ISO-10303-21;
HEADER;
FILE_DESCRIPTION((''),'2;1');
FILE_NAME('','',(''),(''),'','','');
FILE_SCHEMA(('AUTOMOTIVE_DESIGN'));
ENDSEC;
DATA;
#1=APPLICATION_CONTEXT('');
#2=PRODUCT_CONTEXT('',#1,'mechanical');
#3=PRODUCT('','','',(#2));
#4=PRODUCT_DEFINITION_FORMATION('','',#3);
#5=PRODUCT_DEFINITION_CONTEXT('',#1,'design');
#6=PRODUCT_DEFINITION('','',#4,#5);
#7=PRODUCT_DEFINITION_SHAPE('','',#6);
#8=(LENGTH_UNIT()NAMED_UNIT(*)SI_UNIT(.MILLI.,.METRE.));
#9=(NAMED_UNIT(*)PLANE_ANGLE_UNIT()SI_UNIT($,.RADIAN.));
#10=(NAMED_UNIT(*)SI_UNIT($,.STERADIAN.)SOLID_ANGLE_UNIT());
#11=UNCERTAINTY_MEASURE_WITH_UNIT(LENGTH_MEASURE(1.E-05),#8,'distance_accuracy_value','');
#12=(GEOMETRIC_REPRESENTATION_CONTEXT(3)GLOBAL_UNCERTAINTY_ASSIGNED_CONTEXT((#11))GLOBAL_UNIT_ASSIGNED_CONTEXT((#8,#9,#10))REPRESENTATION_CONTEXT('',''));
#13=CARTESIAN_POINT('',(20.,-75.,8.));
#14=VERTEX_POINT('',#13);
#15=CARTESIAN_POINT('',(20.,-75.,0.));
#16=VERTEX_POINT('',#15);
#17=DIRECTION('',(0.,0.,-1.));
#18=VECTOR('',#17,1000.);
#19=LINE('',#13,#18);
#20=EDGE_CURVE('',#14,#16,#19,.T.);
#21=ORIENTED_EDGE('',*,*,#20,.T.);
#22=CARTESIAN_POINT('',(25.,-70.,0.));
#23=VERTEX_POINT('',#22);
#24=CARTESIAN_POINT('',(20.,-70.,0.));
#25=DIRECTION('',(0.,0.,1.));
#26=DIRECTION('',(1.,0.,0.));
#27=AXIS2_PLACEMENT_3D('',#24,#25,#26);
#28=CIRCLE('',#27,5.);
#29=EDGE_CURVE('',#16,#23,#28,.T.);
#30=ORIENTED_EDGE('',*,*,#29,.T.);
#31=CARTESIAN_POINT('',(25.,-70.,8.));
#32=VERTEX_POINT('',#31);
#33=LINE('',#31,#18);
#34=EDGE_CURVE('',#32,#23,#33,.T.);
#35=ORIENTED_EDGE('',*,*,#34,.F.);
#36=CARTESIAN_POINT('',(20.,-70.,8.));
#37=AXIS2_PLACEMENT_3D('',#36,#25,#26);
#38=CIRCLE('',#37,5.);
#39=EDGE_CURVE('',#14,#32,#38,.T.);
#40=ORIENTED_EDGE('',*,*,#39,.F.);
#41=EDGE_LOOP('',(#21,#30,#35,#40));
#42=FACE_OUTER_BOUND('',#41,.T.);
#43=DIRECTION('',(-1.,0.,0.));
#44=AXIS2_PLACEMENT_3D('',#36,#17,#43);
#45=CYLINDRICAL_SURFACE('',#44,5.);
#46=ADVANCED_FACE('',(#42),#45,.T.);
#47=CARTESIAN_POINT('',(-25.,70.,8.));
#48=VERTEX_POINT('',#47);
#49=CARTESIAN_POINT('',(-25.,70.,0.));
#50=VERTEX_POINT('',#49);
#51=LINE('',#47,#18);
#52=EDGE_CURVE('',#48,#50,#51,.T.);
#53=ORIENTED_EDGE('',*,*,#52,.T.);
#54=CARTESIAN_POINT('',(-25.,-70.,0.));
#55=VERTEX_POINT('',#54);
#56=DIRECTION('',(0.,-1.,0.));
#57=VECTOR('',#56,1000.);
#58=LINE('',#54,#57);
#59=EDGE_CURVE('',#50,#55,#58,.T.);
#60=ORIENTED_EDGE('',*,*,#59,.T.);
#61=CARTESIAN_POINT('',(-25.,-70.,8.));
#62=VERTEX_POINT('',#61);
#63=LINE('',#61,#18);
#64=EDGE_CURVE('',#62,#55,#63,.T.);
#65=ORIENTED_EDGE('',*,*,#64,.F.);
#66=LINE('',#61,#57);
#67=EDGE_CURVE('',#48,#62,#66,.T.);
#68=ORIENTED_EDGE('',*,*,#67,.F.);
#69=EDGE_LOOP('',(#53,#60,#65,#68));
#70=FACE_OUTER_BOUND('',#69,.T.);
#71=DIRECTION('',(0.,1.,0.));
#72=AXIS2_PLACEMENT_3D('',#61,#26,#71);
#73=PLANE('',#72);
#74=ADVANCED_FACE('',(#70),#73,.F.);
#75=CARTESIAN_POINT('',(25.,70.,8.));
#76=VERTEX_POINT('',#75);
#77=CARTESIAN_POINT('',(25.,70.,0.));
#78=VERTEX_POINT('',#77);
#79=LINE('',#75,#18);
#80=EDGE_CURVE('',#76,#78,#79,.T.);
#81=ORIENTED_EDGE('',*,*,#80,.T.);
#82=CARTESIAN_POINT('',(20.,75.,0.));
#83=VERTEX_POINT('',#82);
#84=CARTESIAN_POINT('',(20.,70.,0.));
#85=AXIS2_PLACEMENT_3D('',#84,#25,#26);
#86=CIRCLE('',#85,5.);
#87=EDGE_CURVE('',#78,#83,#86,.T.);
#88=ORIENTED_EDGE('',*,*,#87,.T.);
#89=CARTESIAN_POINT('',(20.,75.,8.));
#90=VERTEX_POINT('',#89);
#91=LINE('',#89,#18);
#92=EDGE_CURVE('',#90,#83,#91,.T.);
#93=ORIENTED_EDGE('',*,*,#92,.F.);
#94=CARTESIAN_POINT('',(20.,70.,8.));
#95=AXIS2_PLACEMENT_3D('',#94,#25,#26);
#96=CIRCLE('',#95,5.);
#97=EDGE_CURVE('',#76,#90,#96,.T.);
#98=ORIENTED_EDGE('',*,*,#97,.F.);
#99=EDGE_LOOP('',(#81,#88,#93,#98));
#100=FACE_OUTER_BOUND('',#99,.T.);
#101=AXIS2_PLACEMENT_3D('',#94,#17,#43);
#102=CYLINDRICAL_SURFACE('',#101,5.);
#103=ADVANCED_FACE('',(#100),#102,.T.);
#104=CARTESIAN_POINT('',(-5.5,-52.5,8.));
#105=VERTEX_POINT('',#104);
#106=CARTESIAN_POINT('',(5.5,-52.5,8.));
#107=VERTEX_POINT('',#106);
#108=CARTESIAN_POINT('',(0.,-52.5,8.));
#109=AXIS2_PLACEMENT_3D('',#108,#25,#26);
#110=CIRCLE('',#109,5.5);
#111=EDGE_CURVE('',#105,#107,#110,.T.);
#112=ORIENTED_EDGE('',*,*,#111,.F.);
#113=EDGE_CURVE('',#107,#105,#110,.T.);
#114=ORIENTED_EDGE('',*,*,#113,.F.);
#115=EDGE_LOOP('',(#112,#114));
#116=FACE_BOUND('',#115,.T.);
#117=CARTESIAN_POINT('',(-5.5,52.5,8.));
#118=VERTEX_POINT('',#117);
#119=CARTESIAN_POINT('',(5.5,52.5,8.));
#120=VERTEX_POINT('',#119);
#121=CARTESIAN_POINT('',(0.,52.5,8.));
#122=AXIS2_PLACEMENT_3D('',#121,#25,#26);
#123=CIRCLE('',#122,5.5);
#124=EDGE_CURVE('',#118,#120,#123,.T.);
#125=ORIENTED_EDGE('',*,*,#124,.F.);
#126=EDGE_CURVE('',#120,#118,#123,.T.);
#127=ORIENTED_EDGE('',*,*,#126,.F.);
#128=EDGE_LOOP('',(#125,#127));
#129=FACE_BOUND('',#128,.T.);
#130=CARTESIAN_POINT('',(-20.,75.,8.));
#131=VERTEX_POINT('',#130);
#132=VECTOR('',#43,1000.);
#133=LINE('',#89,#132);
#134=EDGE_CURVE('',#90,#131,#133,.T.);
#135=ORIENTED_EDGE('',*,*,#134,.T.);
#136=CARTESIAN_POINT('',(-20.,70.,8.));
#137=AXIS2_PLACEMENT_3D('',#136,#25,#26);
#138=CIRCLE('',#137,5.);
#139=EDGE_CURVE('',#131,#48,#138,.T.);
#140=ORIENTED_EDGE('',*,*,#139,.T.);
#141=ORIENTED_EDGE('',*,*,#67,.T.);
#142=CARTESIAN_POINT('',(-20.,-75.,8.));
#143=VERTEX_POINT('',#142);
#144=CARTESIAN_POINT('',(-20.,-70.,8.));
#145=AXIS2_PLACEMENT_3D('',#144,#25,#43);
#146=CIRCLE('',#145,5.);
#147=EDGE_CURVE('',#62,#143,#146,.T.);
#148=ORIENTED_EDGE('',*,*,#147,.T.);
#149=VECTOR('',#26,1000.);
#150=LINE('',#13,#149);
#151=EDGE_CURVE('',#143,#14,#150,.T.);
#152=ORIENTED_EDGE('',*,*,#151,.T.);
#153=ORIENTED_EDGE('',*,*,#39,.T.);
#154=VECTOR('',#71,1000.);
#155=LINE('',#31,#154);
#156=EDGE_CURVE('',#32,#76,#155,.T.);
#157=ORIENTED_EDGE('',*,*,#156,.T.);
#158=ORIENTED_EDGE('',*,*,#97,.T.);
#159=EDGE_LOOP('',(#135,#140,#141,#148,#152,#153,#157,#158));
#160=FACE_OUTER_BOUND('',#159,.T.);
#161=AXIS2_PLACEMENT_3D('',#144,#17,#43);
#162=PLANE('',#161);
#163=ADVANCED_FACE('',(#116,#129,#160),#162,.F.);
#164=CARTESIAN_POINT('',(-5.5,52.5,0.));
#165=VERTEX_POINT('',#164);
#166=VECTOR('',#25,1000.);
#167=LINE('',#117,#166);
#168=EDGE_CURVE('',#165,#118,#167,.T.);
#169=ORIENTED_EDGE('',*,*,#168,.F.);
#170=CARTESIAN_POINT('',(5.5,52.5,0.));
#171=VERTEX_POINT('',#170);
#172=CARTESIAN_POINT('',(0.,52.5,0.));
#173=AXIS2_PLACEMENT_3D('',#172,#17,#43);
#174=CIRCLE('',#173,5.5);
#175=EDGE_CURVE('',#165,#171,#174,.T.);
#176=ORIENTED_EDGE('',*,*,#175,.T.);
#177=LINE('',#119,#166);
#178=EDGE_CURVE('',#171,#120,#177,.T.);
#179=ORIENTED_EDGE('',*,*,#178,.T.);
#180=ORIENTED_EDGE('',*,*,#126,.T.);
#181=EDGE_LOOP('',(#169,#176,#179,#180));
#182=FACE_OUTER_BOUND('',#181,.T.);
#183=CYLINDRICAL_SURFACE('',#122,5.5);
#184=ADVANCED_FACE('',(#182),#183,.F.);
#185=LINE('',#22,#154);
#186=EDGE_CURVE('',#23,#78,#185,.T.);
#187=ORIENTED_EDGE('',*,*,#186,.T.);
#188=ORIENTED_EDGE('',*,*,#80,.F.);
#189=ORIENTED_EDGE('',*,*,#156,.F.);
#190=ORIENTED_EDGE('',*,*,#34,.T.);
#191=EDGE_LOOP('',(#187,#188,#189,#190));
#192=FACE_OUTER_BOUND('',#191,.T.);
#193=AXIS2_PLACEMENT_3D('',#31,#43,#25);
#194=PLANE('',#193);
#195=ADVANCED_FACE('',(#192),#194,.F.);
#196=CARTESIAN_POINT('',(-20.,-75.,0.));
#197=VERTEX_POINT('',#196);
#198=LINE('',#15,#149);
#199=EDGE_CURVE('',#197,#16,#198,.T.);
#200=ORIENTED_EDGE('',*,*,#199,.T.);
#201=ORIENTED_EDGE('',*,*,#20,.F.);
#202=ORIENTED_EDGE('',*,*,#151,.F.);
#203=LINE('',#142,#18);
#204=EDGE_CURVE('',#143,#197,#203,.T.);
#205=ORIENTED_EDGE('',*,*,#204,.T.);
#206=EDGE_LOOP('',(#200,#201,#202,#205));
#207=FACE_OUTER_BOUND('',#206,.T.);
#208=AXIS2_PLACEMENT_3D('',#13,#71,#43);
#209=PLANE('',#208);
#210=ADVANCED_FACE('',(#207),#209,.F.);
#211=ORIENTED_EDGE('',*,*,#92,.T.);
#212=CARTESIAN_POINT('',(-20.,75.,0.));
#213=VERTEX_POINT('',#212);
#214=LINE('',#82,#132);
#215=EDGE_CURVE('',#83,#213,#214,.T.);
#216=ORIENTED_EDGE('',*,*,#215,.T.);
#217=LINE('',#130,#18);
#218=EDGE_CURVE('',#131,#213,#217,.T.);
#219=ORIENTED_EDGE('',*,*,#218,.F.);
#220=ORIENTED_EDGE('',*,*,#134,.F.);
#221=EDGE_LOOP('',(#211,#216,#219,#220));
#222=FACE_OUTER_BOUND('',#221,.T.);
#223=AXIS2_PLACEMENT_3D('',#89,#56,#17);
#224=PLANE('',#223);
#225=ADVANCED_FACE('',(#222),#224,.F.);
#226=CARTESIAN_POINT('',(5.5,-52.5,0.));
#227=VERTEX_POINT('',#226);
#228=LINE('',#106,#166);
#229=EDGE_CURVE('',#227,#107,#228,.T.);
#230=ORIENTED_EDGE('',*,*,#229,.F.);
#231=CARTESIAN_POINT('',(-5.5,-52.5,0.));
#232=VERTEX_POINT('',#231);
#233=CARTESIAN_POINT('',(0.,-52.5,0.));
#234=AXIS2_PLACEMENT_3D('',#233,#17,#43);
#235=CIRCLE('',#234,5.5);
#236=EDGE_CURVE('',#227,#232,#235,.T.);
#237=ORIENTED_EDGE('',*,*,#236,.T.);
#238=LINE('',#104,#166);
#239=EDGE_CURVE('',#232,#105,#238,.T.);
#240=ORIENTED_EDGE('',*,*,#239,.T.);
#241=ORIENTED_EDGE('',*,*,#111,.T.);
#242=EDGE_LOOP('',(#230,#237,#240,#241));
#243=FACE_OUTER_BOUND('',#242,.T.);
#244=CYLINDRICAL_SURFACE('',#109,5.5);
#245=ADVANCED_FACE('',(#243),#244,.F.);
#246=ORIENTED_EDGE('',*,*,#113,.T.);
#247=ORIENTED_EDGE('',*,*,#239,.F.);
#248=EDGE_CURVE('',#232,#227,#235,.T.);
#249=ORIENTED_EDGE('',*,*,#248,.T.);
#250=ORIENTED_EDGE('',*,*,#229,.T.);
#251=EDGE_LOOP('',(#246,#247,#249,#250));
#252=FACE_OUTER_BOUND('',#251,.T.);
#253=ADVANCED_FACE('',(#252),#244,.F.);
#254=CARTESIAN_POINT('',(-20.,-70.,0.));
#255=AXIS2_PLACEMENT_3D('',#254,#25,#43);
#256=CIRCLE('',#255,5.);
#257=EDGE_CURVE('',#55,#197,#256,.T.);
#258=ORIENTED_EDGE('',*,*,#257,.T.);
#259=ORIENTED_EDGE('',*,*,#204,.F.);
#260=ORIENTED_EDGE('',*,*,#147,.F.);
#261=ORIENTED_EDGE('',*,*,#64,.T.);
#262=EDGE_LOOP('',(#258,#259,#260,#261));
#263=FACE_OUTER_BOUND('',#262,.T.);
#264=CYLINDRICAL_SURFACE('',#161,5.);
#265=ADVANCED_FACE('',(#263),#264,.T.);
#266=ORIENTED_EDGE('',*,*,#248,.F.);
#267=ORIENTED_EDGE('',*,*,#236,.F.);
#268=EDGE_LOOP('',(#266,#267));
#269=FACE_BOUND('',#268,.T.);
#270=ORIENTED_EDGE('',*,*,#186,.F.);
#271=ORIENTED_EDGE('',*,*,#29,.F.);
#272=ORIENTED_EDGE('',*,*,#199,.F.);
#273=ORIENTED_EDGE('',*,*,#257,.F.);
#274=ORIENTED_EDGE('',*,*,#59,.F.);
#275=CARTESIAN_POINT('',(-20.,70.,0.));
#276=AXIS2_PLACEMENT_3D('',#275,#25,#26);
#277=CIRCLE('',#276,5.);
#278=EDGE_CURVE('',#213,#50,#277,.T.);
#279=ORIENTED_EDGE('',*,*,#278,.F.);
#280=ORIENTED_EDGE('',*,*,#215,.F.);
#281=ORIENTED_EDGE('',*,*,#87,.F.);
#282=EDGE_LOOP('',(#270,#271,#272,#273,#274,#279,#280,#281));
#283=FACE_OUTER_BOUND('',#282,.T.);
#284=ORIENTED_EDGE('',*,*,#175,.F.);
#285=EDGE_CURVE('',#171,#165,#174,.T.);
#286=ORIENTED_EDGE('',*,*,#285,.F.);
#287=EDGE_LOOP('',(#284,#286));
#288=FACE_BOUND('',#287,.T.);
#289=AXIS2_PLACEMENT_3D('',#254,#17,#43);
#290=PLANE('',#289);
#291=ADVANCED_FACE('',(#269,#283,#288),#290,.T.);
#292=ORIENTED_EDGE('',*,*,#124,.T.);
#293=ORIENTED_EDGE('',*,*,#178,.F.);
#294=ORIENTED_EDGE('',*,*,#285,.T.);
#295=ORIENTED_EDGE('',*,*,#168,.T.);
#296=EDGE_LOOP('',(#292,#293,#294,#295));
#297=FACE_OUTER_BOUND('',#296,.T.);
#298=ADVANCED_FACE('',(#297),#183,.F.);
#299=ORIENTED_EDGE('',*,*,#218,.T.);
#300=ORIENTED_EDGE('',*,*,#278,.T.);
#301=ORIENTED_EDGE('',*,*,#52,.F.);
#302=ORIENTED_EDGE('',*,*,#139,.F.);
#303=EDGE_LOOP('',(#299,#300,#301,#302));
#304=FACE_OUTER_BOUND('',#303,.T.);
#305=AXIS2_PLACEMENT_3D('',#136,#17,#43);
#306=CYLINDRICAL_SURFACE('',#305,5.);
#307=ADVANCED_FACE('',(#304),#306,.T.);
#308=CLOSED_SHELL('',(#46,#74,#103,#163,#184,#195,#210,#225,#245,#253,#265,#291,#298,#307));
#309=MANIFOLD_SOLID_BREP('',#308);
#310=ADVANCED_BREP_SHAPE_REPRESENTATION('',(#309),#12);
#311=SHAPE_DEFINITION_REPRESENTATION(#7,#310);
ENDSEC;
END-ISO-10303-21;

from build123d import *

# Parameters (mm, degrees)
BOSS_EXTRUDE1_DEPTH        = 8
F_11_0_11_DIAMETER_HOLE5_D = 11


with BuildPart() as part:
    # Sketch1 → Boss-Extrude1 (new body)
    with BuildSketch(Plane.XY):
        with BuildLine():
            Line((20, -75), (-20, -75))
            ThreePointArc((-20, -75), (-23.535533906, -73.535533906), (-25, -70))
            Line((-25, -70), (-25, 70))
            ThreePointArc((-25, 70), (-23.535533906, 73.535533906), (-20, 75))
            Line((-20, 75), (20, 75))
            ThreePointArc((20, 75), (23.535533906, 73.535533906), (25, 70))
            Line((25, 70), (25, -70))
            ThreePointArc((25, -70), (23.535533906, -73.535533906), (20, -75))
        make_face()
    extrude(amount=BOSS_EXTRUDE1_DEPTH)

    # Ø11.0 (11) Diameter Hole5 (through all)
    with Locations(Plane.XY.offset(8)):
        with Locations((0, 52.5), (0, -52.5)):
            Hole(F_11_0_11_DIAMETER_HOLE5_D / 2)


solid = part.part
